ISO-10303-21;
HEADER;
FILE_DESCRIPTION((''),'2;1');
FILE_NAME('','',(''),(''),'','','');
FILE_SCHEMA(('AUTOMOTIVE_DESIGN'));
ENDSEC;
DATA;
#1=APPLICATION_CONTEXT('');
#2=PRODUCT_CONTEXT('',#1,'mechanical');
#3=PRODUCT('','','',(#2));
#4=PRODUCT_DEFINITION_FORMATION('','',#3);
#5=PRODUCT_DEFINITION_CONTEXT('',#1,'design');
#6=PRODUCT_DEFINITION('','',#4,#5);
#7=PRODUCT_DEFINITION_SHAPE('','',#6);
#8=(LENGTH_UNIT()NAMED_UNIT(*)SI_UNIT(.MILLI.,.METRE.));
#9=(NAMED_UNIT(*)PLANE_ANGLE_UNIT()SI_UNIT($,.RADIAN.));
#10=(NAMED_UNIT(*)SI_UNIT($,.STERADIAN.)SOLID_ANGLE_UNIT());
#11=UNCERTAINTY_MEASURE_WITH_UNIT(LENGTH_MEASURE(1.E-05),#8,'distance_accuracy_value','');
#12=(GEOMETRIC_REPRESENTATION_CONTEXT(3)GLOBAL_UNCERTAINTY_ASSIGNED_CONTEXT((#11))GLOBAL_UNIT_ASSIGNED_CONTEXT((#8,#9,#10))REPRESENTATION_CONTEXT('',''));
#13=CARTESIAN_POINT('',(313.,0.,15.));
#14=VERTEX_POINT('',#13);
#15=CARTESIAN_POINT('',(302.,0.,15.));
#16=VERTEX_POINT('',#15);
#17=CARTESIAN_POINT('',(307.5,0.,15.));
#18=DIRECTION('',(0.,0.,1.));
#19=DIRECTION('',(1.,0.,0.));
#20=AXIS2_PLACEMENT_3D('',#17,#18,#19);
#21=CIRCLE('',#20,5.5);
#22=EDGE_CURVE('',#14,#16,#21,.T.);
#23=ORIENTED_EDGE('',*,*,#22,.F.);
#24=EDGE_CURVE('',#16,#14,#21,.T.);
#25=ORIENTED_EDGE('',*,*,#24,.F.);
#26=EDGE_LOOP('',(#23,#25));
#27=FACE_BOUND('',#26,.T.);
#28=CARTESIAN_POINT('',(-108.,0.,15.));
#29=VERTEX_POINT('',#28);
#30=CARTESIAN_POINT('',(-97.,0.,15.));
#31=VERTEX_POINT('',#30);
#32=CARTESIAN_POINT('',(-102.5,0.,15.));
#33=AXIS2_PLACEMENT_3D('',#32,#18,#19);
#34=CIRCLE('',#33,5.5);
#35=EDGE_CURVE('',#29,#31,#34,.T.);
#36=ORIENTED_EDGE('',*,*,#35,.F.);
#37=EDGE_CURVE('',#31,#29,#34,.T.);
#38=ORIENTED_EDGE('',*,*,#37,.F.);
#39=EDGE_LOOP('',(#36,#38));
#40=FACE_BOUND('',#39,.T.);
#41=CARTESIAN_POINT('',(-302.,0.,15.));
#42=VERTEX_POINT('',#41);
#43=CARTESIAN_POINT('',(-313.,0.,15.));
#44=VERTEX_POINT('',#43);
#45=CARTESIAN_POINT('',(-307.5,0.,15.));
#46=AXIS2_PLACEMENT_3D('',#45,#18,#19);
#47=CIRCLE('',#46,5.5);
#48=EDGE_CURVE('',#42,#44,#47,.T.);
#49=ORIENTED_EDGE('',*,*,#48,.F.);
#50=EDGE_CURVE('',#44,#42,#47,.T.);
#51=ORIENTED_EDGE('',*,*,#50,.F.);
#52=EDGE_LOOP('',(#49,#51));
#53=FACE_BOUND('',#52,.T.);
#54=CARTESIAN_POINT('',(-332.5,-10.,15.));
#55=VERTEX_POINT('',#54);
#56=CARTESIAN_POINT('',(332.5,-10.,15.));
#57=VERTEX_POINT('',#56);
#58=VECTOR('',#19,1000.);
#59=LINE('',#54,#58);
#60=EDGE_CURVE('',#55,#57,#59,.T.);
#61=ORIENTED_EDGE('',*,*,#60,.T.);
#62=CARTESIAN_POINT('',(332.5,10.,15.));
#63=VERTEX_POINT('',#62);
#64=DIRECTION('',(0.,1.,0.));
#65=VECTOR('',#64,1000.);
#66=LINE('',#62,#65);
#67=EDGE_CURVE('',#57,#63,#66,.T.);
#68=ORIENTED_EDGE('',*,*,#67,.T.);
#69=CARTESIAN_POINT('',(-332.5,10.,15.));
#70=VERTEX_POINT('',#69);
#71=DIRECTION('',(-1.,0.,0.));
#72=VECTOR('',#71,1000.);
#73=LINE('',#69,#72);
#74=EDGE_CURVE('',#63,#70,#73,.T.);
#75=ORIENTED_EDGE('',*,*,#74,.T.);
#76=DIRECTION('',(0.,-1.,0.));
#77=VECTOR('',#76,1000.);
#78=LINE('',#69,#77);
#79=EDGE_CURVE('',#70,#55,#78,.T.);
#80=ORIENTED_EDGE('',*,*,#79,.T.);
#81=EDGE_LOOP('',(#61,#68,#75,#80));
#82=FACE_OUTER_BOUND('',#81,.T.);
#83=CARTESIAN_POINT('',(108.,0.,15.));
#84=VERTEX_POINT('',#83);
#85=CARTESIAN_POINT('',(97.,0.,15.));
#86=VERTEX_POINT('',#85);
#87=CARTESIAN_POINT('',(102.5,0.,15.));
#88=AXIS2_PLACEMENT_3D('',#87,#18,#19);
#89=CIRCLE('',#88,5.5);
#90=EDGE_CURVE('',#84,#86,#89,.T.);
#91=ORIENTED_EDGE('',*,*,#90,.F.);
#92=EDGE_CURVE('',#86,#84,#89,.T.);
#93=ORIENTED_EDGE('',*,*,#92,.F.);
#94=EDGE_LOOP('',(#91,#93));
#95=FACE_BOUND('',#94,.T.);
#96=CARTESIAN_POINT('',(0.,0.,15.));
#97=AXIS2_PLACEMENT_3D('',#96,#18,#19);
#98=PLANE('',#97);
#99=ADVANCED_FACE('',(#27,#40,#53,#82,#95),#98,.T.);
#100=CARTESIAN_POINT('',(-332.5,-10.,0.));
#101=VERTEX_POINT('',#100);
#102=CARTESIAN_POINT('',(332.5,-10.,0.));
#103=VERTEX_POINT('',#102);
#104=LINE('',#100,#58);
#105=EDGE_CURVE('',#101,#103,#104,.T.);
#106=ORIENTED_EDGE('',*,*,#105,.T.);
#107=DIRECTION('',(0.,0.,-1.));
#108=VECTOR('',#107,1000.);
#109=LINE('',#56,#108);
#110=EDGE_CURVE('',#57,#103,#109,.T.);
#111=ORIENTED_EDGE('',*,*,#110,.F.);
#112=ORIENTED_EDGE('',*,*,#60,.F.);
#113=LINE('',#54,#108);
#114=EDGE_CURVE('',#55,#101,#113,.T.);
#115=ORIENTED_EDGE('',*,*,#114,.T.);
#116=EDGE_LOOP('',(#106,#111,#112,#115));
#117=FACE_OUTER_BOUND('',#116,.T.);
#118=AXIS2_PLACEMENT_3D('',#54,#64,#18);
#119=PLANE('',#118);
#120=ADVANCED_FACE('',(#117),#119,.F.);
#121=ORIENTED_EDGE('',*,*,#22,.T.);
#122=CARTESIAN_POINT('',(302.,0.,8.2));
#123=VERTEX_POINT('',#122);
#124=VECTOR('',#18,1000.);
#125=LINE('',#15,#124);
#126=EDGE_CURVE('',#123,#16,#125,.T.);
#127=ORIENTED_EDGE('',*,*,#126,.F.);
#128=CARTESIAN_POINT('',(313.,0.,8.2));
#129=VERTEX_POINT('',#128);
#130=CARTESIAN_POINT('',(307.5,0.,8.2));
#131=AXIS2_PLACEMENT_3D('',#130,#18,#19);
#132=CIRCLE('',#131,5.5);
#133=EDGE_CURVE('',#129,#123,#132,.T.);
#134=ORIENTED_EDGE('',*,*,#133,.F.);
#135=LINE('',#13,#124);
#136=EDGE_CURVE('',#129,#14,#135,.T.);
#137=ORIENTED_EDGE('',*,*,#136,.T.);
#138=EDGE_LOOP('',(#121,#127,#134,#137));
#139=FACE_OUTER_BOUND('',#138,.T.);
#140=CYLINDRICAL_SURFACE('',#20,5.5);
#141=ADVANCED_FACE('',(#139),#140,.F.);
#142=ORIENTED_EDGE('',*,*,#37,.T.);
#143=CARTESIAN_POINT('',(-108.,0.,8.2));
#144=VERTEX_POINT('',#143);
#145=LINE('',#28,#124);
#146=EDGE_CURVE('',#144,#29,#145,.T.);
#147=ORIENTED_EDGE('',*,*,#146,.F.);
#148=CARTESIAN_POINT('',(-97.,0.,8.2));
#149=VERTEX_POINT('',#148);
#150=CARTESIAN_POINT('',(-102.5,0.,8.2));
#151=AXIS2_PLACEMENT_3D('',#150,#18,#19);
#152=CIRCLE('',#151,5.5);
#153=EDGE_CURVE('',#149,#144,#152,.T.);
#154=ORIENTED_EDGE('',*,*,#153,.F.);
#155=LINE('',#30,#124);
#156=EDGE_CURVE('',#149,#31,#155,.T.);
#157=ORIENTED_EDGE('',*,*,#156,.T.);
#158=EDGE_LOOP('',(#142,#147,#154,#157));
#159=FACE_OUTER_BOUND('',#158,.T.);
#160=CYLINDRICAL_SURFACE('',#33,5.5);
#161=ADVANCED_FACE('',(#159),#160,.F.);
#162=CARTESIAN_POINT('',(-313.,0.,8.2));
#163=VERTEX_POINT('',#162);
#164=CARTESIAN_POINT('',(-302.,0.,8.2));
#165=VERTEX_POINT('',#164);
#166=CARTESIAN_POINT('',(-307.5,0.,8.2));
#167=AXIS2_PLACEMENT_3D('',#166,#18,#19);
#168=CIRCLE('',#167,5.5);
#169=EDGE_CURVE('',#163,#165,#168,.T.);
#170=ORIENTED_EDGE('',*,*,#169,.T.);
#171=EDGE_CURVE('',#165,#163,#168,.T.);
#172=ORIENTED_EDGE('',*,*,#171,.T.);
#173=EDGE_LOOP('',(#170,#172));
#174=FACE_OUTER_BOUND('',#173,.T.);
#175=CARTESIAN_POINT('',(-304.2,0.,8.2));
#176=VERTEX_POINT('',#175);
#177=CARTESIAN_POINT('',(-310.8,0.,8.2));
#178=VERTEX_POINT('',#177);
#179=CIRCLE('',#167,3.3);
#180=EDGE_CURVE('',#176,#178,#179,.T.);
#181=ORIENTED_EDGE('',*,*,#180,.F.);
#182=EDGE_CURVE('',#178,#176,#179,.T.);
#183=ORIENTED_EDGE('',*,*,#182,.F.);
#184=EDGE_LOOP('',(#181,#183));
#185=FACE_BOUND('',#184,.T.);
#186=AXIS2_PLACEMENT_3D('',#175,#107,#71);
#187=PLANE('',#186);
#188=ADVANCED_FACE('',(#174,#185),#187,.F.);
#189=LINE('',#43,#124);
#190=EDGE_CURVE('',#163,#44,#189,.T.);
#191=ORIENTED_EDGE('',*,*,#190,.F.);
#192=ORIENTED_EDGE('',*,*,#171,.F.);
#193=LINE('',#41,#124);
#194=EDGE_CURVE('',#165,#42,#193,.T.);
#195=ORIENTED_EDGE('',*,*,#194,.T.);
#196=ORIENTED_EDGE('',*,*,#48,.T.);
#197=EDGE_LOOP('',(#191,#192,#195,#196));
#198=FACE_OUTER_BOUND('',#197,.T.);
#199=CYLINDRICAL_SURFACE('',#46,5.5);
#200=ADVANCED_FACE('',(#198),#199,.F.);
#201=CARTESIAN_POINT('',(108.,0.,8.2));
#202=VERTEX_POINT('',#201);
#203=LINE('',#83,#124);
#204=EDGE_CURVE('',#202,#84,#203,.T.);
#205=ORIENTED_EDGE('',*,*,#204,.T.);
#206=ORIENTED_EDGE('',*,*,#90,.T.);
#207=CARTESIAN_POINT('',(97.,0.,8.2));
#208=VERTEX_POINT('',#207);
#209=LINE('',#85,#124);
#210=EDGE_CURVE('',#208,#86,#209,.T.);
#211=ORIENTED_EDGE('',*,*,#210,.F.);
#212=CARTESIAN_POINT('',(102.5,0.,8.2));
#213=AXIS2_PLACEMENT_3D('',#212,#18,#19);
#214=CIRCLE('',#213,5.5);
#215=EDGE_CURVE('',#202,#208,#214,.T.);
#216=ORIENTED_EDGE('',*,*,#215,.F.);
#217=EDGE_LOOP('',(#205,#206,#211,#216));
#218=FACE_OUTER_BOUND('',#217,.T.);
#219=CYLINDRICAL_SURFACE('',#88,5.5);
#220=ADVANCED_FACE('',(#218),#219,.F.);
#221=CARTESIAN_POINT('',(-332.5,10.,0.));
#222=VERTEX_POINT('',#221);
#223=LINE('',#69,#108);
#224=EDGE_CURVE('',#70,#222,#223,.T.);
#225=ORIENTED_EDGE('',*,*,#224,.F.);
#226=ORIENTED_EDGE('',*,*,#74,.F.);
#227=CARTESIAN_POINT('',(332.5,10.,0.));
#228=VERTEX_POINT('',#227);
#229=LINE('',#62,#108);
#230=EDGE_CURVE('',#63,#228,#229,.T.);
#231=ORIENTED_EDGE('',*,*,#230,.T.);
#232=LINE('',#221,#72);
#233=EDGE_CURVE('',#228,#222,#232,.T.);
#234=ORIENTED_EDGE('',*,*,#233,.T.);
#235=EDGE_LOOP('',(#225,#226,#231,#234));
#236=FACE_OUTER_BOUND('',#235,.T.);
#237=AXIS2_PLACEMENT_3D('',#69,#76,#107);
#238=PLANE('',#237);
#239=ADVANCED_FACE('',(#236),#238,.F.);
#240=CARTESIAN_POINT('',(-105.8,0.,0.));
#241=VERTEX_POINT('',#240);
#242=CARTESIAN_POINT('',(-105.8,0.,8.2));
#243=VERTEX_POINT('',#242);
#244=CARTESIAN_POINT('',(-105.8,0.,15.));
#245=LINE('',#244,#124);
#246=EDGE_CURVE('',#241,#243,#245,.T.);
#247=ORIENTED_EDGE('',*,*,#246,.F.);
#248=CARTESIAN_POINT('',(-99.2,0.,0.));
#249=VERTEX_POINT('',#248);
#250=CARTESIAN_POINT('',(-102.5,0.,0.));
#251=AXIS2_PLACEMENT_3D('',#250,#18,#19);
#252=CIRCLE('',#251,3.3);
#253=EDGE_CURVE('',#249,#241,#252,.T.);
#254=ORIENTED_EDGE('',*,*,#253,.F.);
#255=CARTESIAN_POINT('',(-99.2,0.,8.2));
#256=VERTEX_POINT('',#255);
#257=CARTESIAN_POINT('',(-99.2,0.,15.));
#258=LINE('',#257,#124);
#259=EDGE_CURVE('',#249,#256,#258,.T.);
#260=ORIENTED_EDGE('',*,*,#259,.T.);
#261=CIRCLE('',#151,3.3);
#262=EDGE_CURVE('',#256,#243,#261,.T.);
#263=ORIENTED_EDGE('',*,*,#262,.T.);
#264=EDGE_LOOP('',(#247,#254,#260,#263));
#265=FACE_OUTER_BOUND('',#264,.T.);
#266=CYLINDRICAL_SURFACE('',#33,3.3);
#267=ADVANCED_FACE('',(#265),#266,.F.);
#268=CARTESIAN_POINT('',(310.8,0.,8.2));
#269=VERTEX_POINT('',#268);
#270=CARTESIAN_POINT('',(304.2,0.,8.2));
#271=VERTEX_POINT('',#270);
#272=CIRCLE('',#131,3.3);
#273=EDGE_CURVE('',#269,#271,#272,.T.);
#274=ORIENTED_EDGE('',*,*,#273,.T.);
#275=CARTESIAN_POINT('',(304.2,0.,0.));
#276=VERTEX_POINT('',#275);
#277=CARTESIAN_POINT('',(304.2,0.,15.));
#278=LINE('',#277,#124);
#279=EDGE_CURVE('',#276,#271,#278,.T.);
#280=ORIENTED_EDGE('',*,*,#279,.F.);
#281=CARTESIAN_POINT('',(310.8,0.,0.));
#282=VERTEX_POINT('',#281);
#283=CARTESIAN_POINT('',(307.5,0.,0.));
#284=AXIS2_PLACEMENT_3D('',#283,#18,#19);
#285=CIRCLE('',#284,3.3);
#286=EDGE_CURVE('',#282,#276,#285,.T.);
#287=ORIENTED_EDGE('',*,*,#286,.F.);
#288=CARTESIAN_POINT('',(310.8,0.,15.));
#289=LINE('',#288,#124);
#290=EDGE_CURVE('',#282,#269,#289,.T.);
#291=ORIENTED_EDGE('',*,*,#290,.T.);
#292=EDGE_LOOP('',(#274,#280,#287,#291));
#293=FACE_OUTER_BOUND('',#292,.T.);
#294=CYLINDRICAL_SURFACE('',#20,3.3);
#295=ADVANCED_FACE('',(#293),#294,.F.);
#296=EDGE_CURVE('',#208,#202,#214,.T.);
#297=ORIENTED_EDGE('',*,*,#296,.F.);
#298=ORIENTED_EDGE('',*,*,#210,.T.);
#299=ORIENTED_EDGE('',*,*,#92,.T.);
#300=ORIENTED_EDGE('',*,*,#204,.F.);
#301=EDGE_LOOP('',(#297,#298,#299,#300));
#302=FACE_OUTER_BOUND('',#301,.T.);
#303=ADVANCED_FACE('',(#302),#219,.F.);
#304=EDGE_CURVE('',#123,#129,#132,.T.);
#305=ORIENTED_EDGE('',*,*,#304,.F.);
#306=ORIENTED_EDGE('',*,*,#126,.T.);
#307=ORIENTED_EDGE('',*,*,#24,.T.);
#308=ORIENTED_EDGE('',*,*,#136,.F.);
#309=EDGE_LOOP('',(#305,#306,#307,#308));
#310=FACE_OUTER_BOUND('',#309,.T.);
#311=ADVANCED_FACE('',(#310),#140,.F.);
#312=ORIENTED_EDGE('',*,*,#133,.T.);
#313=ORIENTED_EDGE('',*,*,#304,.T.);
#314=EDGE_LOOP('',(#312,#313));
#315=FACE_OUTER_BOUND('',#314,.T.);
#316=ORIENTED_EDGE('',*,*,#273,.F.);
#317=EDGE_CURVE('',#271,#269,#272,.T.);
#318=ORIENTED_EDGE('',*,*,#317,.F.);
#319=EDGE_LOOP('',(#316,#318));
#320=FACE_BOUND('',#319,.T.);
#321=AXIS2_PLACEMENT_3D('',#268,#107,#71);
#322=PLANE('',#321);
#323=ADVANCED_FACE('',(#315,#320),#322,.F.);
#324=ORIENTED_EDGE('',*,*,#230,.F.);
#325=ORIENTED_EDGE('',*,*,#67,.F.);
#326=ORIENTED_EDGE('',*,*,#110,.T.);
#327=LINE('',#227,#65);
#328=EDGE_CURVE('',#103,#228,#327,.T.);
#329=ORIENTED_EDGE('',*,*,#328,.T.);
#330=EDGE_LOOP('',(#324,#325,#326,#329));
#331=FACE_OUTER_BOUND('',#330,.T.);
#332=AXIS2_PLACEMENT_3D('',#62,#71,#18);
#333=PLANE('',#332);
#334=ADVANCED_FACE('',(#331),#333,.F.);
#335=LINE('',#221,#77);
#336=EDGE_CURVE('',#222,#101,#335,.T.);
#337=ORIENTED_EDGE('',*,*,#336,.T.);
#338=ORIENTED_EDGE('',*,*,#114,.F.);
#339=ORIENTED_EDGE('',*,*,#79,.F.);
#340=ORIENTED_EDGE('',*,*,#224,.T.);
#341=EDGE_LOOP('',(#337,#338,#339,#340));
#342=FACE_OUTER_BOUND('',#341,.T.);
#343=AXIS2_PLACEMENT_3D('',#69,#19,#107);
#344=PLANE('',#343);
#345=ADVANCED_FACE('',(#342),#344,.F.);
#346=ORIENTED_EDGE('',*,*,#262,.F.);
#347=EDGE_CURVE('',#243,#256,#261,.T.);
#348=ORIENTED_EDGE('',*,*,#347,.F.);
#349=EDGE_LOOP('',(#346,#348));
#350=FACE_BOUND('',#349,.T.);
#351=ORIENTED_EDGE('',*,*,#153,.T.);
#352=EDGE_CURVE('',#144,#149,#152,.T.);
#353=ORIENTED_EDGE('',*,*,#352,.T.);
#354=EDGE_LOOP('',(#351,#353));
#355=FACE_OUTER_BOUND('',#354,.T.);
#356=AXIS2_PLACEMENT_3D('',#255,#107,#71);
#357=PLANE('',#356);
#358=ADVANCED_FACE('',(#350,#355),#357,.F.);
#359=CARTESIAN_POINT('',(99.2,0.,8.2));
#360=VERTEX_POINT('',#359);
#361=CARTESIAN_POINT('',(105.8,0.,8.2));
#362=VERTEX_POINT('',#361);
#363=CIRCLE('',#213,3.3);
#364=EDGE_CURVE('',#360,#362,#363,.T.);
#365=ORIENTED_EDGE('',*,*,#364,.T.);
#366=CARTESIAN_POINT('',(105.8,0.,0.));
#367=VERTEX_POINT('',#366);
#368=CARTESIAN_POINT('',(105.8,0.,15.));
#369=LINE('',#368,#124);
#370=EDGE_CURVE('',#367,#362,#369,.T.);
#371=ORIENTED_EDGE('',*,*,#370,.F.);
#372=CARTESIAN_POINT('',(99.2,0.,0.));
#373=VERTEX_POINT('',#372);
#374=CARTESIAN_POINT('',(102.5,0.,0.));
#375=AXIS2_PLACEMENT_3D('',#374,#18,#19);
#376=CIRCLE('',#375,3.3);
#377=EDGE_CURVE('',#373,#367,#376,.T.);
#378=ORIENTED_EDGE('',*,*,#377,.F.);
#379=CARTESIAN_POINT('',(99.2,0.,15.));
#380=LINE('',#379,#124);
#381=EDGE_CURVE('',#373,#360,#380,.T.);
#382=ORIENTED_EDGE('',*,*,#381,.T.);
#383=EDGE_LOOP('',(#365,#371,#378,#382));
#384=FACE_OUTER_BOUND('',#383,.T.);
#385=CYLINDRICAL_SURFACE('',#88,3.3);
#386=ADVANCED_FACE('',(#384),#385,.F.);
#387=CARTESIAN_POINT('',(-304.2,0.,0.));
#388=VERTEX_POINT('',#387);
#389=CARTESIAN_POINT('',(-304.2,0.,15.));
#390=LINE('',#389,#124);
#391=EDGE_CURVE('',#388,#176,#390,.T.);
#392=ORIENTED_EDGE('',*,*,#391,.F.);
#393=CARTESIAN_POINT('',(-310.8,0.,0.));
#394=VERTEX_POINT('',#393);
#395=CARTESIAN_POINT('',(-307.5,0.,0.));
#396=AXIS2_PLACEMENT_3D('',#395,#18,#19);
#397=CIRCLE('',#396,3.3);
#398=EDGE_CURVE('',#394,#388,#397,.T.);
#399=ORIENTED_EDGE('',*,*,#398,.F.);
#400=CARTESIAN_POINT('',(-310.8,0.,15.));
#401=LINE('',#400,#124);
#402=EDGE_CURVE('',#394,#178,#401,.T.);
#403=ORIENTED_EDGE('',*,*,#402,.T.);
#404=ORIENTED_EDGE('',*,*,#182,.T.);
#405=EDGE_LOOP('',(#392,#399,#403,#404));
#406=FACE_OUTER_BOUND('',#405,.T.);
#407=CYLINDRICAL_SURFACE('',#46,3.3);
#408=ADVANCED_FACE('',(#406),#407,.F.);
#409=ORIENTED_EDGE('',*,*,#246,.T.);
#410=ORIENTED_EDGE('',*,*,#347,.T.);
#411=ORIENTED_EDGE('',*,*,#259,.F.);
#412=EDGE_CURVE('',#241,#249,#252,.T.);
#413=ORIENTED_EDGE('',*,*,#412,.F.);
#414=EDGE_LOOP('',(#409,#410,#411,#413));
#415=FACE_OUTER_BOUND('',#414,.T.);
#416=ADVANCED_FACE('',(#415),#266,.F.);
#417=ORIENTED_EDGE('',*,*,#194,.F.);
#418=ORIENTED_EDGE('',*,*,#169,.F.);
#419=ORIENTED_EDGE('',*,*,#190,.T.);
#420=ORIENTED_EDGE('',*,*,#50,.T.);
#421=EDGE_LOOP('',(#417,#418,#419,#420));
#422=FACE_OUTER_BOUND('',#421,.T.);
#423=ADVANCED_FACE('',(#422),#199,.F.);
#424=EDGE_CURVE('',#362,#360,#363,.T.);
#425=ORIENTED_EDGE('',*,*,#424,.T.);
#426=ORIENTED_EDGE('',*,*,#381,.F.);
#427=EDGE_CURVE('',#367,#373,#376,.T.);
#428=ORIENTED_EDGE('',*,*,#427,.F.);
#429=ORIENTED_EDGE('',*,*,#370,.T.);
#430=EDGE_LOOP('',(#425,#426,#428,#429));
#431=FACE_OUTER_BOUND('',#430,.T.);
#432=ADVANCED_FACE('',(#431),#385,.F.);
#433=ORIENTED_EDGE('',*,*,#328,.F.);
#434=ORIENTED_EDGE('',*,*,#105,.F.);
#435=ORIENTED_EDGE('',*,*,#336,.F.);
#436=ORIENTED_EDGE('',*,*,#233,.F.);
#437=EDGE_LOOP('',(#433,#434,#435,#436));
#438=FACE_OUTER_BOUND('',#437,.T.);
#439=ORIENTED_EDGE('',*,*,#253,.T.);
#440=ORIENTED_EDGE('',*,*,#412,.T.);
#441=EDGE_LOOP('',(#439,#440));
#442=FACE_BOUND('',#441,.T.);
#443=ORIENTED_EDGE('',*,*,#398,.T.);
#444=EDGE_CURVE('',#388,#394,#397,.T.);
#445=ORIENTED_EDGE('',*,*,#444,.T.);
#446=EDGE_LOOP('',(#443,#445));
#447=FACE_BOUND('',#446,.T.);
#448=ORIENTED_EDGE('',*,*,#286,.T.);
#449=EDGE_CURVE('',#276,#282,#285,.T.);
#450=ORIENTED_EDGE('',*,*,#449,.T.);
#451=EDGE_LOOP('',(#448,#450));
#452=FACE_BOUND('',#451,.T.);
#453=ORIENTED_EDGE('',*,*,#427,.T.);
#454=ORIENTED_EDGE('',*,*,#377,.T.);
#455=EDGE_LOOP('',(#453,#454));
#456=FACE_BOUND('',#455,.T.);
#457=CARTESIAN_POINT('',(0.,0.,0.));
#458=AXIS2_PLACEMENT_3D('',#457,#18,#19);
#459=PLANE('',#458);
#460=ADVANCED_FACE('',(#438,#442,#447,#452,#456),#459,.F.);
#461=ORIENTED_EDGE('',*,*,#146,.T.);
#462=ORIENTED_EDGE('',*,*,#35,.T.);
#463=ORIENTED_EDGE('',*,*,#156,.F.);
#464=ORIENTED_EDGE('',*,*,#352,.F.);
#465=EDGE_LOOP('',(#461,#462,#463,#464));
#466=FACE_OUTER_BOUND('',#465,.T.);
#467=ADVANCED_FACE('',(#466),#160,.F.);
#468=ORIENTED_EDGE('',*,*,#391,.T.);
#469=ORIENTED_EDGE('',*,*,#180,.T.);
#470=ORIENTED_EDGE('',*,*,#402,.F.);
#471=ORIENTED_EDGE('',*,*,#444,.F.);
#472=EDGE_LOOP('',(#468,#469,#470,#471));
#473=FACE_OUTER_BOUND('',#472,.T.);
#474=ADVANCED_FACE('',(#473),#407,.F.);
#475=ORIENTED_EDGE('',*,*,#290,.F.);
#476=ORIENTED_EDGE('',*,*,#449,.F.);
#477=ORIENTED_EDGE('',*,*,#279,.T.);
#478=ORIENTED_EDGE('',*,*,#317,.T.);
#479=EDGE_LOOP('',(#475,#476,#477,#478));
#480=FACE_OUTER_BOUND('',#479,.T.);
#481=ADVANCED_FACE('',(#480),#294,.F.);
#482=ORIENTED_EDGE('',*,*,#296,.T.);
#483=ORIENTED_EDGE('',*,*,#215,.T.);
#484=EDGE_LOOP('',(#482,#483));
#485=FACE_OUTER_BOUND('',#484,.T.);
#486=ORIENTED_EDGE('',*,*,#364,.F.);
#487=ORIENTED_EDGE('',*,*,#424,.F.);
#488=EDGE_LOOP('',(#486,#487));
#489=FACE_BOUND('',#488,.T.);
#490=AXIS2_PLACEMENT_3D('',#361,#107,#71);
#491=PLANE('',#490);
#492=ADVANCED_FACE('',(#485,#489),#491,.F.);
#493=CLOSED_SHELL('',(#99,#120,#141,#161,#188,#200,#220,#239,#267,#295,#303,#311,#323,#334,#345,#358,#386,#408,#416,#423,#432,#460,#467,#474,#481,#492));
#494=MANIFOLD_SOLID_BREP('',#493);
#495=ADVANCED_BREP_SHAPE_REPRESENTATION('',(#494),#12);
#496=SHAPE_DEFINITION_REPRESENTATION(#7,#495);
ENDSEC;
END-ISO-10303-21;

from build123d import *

# Parameters (mm, degrees)
SKETCH_1_W                = 665
SKETCH_1_H                = 20
EXTRUDE_1_DEPTH           = 15
HOLE_WIZARD_1_D           = 6.6
HOLE_WIZARD_1_CBORE_D     = 11
HOLE_WIZARD_1_CBORE_DEPTH = 6.8


with BuildPart() as part:
    # 草图1 → 凸台-拉伸1 (new body)
    with BuildSketch(Plane.XY):
        Rectangle(SKETCH_1_W, SKETCH_1_H)
    extrude(amount=EXTRUDE_1_DEPTH)

    # 打孔尺寸(%根据)内六角圆柱头螺钉的类型1 (through all)
    with Locations(Plane.XY.offset(15)):
        with Locations((102.5, 0), (-307.5, 0), (307.5, 0), (-102.5, 0)):
            CounterBoreHole(HOLE_WIZARD_1_D / 2, HOLE_WIZARD_1_CBORE_D / 2, HOLE_WIZARD_1_CBORE_DEPTH)


solid = part.part
